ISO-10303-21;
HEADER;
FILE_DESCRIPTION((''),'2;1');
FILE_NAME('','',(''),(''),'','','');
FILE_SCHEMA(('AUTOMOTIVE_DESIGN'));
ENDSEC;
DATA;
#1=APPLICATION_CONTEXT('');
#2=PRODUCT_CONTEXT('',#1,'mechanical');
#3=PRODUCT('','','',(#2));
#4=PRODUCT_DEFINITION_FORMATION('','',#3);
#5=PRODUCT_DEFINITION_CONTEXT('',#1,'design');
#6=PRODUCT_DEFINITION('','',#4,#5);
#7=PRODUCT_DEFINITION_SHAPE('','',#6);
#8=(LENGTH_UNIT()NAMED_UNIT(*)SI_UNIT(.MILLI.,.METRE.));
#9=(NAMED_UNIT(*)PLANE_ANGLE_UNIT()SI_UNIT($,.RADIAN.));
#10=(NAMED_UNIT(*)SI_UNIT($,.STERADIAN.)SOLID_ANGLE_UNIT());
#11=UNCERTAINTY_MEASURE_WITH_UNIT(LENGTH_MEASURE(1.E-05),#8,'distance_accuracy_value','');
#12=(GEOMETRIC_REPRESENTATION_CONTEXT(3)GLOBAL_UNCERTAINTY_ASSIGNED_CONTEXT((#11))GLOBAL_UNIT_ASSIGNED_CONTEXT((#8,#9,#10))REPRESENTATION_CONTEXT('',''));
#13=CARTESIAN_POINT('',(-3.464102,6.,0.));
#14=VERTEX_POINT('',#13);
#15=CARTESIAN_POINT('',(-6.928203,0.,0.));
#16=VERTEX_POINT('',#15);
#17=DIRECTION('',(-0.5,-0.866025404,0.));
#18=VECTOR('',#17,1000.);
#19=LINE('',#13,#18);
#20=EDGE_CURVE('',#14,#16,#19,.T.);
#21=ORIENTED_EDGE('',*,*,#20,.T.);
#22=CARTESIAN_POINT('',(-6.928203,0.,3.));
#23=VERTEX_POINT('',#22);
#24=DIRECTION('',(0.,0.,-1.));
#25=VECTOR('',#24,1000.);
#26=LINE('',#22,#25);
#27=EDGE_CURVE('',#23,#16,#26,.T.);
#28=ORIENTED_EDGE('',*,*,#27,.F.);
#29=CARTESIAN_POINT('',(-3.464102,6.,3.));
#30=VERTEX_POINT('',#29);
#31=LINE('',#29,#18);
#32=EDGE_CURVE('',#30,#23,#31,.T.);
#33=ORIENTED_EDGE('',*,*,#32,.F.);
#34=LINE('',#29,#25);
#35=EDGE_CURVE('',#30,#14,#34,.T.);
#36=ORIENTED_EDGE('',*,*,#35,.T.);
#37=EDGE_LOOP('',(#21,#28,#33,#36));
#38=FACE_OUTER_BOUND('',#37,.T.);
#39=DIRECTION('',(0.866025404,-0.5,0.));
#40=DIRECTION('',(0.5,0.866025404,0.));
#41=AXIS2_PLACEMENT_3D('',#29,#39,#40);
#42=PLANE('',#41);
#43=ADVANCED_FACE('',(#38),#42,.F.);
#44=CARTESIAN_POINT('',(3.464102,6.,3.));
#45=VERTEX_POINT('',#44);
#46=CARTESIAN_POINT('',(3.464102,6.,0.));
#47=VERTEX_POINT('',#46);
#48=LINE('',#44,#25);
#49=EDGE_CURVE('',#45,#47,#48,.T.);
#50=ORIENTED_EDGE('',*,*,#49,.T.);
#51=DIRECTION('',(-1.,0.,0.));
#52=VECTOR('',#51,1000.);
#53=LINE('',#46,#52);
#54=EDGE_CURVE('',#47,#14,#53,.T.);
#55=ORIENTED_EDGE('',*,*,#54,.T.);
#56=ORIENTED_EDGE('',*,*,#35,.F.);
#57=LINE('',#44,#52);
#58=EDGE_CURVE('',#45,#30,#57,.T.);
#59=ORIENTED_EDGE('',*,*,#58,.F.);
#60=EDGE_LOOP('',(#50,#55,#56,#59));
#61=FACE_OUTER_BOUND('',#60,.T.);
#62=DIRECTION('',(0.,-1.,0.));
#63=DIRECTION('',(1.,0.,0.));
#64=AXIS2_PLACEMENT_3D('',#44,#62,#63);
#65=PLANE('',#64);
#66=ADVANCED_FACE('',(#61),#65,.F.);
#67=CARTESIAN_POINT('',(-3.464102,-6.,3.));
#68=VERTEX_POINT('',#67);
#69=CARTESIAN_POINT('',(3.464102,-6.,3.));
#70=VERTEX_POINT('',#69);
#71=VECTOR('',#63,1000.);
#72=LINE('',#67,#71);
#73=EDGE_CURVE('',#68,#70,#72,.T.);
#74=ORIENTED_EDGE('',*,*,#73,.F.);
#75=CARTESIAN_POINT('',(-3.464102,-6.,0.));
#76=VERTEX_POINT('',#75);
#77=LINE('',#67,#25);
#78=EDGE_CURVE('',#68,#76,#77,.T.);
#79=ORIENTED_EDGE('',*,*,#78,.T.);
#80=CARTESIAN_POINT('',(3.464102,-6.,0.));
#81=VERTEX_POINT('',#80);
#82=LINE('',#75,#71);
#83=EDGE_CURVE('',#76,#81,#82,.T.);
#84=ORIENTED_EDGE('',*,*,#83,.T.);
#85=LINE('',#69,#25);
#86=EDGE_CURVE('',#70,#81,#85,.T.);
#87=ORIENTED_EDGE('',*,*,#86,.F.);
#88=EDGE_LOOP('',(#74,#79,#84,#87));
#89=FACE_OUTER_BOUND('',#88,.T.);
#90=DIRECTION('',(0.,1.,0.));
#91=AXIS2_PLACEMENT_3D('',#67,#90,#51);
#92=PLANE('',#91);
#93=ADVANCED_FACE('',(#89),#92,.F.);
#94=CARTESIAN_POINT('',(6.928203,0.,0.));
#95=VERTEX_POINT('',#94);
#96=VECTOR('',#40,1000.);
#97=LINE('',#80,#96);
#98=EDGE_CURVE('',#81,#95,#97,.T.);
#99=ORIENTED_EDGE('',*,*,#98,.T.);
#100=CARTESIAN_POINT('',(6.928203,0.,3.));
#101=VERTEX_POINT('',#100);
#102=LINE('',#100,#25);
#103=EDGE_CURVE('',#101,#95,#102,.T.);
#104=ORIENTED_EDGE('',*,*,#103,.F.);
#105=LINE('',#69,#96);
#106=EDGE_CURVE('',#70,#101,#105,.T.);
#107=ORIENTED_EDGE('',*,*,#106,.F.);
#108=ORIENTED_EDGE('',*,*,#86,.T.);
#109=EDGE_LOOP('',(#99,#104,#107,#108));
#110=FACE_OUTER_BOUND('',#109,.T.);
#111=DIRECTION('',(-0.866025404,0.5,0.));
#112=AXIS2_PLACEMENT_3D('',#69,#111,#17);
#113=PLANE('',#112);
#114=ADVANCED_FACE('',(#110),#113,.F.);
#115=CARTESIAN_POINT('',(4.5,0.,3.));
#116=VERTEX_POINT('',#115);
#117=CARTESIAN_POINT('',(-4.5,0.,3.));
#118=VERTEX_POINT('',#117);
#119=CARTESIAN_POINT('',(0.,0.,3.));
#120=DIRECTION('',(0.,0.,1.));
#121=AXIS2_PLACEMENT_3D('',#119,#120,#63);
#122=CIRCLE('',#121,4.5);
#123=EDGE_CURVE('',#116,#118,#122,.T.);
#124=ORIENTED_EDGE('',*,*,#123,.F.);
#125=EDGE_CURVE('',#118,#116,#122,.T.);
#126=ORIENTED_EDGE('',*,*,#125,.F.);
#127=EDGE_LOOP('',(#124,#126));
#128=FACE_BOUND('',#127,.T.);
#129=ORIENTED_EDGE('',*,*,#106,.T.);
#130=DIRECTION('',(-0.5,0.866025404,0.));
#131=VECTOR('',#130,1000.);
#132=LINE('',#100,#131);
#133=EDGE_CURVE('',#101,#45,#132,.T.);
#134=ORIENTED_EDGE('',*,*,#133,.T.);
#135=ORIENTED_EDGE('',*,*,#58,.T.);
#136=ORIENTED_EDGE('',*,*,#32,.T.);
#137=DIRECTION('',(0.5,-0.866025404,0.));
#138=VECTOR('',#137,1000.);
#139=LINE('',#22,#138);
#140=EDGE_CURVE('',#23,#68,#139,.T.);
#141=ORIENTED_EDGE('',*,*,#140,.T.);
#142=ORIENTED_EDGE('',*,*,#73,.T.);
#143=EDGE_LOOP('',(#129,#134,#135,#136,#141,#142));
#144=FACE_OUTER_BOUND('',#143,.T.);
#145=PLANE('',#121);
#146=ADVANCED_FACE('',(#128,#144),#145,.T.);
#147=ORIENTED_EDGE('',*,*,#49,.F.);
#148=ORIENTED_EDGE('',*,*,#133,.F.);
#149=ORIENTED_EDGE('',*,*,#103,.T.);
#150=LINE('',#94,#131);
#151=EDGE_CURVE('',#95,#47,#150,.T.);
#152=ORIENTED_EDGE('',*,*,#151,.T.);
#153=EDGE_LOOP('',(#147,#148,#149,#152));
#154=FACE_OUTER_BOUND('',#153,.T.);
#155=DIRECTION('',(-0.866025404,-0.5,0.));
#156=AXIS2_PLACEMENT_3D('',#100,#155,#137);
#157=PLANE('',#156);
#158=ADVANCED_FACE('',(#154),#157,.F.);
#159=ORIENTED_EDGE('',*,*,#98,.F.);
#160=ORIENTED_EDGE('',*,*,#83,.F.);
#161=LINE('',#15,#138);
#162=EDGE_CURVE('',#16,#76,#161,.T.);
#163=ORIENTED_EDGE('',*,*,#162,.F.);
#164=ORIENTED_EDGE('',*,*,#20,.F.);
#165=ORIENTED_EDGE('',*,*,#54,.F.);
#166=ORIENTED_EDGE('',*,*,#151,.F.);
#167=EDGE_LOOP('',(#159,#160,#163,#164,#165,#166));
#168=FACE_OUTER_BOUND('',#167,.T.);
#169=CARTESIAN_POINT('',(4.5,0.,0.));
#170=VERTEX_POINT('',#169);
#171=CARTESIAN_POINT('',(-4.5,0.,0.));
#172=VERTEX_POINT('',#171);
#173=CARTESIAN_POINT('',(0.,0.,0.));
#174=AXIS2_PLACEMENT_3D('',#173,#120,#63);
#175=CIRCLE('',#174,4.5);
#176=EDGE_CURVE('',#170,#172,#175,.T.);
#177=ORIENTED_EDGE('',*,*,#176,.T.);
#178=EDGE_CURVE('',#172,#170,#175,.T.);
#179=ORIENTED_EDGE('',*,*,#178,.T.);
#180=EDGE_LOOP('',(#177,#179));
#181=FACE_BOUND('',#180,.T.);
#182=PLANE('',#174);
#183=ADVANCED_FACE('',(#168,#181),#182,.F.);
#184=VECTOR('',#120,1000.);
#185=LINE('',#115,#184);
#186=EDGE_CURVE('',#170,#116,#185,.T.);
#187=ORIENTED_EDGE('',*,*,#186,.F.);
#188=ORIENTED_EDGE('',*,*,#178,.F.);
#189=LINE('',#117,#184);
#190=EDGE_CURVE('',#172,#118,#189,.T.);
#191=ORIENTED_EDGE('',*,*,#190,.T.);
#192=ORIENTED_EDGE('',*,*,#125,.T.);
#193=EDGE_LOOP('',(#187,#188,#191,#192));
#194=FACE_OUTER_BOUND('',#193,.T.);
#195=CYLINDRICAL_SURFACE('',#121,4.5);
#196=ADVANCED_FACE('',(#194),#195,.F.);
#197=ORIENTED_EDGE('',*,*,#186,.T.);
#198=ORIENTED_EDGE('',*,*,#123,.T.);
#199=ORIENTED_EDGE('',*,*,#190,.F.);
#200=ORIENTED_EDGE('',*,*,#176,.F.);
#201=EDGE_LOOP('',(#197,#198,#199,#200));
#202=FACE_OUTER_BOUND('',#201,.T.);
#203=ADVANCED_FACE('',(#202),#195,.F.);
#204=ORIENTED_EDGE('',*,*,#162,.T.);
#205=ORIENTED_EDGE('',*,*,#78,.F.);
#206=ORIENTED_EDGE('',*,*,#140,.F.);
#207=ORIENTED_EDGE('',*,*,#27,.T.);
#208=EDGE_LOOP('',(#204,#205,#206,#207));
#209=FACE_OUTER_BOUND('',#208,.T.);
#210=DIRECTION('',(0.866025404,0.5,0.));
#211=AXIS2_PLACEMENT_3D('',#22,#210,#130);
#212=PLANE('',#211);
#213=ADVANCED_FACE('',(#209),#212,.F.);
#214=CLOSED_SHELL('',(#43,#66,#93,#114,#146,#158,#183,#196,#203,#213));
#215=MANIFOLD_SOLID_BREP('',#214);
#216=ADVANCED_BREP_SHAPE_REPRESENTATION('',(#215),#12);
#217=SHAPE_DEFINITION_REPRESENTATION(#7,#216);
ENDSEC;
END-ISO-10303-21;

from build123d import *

# Parameters (mm, degrees)
BOSS_EXTRUDE1_DEPTH        = 3
M10X1_0_TAPPED_HOLE1_D     = 9
M10X1_0_TAPPED_HOLE1_DEPTH = 23
M10X1_0_TAPPED_HOLE1_TIP   = 2.703872786


with BuildPart() as part:
    # Sketch1 → Boss-Extrude1 (new body)
    with BuildSketch(Plane.XY):
        Polygon((6.92820323, 0), (3.464101615, 6), (-3.464101615, 6), (-6.92820323, 0), (-3.464101615, -6), (3.464101615, -6), align=None)
    extrude(amount=BOSS_EXTRUDE1_DEPTH)

    # M10x1.0 Tapped Hole1
    with Locations(Plane.XY.offset(3)):
        with Locations((0, 0)):
            Hole(M10X1_0_TAPPED_HOLE1_D / 2, depth=M10X1_0_TAPPED_HOLE1_DEPTH)
            with Locations((0, 0, -(M10X1_0_TAPPED_HOLE1_DEPTH + M10X1_0_TAPPED_HOLE1_TIP / 2))):  # 118° drill point
                Cone(0, M10X1_0_TAPPED_HOLE1_D / 2, M10X1_0_TAPPED_HOLE1_TIP, mode=Mode.SUBTRACT)


solid = part.part
